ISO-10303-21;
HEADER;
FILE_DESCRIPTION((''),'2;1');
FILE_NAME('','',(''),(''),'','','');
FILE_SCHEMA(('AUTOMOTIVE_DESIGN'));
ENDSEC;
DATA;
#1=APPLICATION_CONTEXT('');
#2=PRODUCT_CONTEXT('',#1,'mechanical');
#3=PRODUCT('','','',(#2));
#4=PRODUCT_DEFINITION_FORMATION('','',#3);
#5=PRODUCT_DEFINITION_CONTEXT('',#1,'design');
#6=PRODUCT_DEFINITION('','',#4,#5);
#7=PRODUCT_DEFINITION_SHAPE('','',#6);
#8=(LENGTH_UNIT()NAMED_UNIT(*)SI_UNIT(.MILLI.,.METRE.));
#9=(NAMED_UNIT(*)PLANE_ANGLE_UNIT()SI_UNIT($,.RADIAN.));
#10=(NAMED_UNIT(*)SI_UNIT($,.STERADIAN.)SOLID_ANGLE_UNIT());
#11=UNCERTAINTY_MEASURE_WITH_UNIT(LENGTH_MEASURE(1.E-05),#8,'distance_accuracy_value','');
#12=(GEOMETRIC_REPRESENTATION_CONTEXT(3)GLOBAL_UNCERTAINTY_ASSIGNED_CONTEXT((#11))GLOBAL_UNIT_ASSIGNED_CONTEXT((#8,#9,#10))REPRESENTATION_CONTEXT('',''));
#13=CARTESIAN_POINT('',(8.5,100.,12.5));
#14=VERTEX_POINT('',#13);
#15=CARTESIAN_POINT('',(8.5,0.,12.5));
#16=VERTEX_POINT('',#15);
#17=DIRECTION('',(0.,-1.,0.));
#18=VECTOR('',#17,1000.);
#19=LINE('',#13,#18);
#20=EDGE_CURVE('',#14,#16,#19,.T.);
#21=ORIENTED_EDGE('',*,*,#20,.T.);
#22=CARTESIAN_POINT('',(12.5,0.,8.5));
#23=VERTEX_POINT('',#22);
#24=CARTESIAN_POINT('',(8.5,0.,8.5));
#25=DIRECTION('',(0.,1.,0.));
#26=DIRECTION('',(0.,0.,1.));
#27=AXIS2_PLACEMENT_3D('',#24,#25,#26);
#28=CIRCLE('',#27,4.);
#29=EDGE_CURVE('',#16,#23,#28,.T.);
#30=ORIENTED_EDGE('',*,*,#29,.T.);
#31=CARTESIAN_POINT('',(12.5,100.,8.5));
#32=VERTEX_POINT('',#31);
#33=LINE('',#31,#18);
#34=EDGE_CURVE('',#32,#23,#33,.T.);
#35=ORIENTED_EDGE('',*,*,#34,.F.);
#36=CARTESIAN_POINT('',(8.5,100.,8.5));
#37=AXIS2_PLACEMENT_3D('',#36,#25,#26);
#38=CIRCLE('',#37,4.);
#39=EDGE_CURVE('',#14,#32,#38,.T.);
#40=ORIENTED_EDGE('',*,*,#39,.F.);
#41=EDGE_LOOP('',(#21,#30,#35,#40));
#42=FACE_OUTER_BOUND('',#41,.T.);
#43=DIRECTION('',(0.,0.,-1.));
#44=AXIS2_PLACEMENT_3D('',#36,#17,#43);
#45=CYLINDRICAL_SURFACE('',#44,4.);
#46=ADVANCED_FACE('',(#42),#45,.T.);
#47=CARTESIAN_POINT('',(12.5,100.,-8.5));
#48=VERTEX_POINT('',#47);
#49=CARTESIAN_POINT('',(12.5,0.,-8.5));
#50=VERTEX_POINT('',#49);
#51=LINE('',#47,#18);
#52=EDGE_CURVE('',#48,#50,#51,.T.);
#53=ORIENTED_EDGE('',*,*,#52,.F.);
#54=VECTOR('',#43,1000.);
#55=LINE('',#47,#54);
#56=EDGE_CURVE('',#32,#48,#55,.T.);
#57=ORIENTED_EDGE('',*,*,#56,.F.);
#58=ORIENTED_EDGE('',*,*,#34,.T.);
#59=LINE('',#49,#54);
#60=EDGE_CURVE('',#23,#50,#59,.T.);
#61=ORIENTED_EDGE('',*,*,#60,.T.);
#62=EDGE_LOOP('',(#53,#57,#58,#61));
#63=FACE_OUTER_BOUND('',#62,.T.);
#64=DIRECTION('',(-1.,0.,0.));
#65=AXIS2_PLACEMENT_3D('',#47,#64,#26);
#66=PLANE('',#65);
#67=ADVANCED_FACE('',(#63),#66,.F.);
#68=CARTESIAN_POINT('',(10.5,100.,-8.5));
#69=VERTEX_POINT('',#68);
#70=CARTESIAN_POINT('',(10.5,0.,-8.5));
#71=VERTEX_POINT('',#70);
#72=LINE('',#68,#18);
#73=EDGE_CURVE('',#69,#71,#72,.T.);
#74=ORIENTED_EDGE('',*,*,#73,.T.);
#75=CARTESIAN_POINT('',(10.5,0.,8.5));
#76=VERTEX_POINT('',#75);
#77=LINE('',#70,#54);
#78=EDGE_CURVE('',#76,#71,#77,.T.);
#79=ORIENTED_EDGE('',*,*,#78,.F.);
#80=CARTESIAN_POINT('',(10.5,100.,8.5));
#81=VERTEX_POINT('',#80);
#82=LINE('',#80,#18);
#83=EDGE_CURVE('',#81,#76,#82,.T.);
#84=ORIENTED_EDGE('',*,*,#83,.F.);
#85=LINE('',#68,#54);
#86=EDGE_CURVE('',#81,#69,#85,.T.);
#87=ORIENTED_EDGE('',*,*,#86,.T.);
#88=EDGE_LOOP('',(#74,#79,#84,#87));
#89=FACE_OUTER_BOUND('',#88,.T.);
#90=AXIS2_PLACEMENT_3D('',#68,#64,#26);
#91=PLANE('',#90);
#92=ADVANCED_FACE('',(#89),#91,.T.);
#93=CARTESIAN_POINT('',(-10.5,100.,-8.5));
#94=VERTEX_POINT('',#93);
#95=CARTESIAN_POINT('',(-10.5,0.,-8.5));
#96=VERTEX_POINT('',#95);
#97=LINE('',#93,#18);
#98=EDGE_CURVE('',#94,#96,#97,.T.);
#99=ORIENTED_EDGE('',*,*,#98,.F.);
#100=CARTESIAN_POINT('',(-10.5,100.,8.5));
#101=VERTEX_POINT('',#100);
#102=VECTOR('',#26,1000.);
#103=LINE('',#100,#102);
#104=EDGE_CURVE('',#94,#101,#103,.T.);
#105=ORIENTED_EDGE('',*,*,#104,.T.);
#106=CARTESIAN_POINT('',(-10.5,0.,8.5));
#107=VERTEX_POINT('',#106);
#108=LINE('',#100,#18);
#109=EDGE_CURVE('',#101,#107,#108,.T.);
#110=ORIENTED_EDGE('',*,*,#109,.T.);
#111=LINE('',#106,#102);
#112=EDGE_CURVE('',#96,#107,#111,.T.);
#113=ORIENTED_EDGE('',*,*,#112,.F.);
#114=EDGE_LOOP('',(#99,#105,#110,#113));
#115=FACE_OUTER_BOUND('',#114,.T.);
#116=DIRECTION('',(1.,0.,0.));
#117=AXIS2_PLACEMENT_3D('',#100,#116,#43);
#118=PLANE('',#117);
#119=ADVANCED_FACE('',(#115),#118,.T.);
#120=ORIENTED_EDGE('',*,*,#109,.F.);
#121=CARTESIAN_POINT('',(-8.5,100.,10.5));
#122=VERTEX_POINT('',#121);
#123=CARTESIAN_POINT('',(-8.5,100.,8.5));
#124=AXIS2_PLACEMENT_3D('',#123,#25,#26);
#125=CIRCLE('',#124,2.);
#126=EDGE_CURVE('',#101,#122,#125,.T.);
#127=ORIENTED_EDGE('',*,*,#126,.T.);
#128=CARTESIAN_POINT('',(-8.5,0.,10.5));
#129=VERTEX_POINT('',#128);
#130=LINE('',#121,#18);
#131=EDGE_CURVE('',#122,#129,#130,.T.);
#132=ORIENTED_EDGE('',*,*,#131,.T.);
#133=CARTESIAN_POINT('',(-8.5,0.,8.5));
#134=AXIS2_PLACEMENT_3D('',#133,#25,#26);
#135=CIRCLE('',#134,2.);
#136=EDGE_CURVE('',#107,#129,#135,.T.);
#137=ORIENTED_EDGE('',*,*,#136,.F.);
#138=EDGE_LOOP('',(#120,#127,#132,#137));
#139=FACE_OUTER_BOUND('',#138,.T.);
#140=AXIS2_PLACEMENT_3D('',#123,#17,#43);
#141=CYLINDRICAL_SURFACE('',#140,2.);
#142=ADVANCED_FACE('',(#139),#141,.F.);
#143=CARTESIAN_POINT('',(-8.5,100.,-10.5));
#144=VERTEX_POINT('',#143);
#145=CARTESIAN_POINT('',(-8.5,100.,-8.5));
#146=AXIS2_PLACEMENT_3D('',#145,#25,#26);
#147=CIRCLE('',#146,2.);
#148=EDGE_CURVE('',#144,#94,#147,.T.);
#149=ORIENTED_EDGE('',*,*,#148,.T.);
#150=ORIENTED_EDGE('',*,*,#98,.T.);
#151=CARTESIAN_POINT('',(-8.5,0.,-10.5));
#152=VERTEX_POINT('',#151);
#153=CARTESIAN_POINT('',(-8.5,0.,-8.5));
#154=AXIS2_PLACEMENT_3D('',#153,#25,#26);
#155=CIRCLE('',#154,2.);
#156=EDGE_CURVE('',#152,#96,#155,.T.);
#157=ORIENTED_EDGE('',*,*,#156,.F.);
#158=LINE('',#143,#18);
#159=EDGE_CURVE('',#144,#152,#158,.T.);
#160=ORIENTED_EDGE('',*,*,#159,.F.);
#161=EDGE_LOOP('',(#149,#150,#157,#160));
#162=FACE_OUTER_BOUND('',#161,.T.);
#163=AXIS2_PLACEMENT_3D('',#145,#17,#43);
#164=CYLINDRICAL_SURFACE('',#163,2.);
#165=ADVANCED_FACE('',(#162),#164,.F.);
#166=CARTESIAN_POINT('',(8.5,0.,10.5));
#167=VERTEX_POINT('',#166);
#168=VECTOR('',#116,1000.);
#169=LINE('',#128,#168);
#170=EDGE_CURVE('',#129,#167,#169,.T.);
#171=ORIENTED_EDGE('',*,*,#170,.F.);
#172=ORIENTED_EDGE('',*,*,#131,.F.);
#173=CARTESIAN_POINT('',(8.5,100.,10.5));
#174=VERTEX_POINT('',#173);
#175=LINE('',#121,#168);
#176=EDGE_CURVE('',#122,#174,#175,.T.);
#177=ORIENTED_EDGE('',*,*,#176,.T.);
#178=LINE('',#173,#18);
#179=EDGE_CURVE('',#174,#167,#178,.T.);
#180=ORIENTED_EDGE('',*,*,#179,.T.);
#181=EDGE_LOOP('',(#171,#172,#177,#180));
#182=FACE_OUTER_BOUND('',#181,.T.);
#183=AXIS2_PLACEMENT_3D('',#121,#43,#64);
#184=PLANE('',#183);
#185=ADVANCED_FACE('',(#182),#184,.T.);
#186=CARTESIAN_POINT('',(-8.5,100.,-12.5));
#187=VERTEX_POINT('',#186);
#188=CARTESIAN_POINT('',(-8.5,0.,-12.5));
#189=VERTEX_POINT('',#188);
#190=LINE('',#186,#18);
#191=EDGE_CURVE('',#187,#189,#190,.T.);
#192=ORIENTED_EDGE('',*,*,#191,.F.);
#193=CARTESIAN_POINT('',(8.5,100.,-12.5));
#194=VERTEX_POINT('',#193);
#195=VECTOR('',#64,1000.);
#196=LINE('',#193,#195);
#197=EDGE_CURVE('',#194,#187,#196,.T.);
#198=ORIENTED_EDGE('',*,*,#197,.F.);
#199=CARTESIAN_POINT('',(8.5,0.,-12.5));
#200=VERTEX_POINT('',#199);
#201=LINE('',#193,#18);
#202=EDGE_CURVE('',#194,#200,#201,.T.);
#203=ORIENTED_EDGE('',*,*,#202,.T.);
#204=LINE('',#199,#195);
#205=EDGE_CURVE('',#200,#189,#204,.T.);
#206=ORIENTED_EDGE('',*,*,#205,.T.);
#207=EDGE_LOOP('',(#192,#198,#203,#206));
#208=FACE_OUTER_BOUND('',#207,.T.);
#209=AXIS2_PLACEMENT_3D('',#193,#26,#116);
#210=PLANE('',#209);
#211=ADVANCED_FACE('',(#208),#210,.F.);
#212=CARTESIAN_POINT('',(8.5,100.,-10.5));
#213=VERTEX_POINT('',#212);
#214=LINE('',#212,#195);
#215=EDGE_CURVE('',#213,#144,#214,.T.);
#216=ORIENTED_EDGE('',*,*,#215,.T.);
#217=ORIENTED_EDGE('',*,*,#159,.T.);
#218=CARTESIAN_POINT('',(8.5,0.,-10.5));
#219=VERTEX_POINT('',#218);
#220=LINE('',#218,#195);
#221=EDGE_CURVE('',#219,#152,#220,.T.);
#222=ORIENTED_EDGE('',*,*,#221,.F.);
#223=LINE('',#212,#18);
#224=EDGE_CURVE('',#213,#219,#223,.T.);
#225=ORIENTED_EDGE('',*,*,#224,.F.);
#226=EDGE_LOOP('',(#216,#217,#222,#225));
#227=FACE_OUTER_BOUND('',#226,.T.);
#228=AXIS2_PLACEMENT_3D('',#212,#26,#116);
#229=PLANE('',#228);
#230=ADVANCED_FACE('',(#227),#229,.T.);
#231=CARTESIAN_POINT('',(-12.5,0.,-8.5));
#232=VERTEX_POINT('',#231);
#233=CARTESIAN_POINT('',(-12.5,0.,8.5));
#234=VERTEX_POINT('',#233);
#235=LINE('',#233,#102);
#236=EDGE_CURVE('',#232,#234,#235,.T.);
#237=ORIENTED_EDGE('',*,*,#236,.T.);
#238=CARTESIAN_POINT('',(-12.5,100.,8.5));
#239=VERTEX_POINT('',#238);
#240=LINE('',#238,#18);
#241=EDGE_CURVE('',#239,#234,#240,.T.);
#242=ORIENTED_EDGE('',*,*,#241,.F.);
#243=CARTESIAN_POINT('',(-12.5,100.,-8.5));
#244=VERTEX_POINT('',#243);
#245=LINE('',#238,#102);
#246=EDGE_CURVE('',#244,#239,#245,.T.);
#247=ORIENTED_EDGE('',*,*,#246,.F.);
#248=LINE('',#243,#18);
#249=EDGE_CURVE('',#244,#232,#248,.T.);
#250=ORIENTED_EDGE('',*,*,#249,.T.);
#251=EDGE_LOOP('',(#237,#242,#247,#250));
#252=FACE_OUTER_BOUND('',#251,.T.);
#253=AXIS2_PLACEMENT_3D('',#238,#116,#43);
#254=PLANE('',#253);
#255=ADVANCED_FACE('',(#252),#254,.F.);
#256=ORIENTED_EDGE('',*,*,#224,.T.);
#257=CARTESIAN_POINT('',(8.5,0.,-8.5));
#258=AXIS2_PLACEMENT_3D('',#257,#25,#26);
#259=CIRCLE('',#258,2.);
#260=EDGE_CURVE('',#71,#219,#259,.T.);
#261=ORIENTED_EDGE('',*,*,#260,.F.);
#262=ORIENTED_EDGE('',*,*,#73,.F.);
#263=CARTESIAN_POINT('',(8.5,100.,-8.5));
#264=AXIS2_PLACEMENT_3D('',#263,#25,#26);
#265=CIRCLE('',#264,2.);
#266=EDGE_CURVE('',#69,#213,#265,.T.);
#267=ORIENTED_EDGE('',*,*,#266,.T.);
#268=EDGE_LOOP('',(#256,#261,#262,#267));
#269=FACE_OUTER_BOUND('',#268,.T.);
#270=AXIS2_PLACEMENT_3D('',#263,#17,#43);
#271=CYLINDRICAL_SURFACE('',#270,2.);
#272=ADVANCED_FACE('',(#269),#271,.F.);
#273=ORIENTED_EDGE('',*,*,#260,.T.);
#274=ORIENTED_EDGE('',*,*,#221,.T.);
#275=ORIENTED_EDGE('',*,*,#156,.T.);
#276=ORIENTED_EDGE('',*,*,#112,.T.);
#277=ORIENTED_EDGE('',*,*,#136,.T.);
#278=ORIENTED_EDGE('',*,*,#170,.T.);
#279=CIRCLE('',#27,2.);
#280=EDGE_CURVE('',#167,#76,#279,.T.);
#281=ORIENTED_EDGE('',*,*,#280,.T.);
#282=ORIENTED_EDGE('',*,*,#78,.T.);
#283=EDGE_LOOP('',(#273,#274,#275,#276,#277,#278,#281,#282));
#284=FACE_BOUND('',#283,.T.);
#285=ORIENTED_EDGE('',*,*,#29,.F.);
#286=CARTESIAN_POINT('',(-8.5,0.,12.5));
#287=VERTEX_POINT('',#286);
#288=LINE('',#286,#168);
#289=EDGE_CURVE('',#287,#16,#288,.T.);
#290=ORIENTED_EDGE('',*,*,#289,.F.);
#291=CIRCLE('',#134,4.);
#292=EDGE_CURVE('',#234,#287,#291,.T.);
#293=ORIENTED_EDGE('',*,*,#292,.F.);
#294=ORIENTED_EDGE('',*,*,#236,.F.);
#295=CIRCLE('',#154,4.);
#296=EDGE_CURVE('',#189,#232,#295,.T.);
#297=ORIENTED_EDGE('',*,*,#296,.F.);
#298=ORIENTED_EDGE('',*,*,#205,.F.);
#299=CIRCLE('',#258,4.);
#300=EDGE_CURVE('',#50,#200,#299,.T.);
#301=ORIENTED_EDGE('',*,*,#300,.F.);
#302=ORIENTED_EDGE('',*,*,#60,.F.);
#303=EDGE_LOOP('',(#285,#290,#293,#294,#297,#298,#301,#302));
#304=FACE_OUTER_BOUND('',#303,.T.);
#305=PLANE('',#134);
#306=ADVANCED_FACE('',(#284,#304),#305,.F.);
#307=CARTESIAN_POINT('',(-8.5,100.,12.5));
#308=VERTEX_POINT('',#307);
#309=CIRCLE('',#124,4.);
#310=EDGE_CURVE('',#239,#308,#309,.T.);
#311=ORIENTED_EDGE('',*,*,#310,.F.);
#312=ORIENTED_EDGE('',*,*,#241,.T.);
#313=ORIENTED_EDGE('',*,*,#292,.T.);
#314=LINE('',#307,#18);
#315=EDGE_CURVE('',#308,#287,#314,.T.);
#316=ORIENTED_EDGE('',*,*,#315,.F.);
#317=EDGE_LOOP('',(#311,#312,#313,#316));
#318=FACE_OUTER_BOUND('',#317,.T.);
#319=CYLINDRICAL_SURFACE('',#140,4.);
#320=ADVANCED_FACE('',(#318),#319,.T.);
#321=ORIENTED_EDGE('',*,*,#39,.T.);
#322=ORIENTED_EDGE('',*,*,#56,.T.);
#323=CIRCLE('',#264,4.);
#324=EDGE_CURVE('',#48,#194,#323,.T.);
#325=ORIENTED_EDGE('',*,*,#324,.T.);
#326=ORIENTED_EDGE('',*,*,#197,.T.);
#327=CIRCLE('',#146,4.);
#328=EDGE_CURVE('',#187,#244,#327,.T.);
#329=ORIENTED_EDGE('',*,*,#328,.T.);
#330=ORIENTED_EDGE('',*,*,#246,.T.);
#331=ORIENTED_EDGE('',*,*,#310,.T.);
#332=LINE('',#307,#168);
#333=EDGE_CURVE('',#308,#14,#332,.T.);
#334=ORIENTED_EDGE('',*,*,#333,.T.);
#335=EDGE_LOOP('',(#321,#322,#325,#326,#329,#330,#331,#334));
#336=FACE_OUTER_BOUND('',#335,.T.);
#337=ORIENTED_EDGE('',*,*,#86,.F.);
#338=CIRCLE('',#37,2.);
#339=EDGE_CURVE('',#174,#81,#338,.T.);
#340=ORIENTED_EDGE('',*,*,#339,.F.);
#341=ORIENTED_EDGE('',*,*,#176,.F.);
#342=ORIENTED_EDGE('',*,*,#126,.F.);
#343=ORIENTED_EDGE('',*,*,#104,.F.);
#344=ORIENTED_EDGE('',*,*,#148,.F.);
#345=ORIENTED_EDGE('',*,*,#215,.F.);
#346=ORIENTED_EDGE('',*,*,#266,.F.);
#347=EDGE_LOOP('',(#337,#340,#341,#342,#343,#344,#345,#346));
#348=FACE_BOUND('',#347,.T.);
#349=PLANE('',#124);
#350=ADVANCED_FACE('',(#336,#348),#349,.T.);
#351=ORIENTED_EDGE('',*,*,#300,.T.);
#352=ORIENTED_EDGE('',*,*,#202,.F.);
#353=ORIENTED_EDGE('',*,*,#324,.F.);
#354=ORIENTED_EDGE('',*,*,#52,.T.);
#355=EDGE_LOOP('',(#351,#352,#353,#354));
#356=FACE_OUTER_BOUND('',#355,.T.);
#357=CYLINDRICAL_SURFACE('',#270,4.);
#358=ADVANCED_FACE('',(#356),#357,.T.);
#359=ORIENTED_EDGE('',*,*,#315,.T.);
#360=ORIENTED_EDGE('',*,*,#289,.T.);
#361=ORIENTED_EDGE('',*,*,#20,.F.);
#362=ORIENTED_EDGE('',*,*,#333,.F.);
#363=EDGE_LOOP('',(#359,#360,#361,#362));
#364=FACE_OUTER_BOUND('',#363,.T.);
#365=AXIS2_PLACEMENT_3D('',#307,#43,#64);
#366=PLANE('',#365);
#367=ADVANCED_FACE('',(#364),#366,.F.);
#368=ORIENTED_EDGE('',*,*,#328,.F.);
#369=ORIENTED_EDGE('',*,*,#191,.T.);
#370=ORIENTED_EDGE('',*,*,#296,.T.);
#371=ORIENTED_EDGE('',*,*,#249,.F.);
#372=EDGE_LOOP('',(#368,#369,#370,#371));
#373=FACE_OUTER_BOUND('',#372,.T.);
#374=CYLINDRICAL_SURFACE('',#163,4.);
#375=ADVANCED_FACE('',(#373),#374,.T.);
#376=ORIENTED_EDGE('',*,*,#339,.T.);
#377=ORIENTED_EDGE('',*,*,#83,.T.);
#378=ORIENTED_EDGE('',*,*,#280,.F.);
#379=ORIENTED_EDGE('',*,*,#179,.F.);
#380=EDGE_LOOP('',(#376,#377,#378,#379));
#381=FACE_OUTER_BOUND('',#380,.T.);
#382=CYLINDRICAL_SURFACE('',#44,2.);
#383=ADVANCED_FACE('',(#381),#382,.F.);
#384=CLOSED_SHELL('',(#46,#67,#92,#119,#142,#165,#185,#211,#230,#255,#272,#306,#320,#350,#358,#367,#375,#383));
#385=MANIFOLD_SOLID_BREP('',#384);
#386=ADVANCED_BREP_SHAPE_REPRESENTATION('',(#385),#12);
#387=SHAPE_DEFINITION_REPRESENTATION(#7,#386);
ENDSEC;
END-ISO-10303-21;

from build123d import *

# Parameters (mm, degrees)
GB_T_6728_2002_SQUARE_HOLLOW_SECTION_STE_DEPTH = 100


with BuildPart() as part:
    # Sketch14 → Gb／t 6728—2002 Square hollow section steel 25×2-example.com(1) (new body)
    with BuildSketch(Plane(origin=(0, 0, 0), x_dir=(-1, 0, 0), z_dir=(0, 1, 0))):
        with BuildLine():
            Line((-8.5, -12.5), (8.5, -12.5))
            ThreePointArc((8.5, -12.5), (11.328427125, -11.328427125), (12.5, -8.5))
            Line((12.5, -8.5), (12.5, 8.5))
            ThreePointArc((12.5, 8.5), (11.328427125, 11.328427125), (8.5, 12.5))
            Line((8.5, 12.5), (-8.5, 12.5))
            ThreePointArc((-8.5, 12.5), (-11.328427125, 11.328427125), (-12.5, 8.5))
            Line((-12.5, 8.5), (-12.5, -8.5))
            ThreePointArc((-12.5, -8.5), (-11.328427125, -11.328427125), (-8.5, -12.5))
        make_face()
        with BuildLine():
            Line((-8.5, -10.5), (8.5, -10.5))
            ThreePointArc((8.5, -10.5), (9.914213562, -9.914213562), (10.5, -8.5))
            Line((10.5, -8.5), (10.5, 8.5))
            ThreePointArc((10.5, 8.5), (9.914213562, 9.914213562), (8.5, 10.5))
            Line((8.5, 10.5), (-8.5, 10.5))
            ThreePointArc((-8.5, 10.5), (-9.914213562, 9.914213562), (-10.5, 8.5))
            Line((-10.5, 8.5), (-10.5, -8.5))
            ThreePointArc((-10.5, -8.5), (-9.914213562, -9.914213562), (-8.5, -10.5))
        make_face(mode=Mode.SUBTRACT)
    extrude(amount=GB_T_6728_2002_SQUARE_HOLLOW_SECTION_STE_DEPTH)


solid = part.part
